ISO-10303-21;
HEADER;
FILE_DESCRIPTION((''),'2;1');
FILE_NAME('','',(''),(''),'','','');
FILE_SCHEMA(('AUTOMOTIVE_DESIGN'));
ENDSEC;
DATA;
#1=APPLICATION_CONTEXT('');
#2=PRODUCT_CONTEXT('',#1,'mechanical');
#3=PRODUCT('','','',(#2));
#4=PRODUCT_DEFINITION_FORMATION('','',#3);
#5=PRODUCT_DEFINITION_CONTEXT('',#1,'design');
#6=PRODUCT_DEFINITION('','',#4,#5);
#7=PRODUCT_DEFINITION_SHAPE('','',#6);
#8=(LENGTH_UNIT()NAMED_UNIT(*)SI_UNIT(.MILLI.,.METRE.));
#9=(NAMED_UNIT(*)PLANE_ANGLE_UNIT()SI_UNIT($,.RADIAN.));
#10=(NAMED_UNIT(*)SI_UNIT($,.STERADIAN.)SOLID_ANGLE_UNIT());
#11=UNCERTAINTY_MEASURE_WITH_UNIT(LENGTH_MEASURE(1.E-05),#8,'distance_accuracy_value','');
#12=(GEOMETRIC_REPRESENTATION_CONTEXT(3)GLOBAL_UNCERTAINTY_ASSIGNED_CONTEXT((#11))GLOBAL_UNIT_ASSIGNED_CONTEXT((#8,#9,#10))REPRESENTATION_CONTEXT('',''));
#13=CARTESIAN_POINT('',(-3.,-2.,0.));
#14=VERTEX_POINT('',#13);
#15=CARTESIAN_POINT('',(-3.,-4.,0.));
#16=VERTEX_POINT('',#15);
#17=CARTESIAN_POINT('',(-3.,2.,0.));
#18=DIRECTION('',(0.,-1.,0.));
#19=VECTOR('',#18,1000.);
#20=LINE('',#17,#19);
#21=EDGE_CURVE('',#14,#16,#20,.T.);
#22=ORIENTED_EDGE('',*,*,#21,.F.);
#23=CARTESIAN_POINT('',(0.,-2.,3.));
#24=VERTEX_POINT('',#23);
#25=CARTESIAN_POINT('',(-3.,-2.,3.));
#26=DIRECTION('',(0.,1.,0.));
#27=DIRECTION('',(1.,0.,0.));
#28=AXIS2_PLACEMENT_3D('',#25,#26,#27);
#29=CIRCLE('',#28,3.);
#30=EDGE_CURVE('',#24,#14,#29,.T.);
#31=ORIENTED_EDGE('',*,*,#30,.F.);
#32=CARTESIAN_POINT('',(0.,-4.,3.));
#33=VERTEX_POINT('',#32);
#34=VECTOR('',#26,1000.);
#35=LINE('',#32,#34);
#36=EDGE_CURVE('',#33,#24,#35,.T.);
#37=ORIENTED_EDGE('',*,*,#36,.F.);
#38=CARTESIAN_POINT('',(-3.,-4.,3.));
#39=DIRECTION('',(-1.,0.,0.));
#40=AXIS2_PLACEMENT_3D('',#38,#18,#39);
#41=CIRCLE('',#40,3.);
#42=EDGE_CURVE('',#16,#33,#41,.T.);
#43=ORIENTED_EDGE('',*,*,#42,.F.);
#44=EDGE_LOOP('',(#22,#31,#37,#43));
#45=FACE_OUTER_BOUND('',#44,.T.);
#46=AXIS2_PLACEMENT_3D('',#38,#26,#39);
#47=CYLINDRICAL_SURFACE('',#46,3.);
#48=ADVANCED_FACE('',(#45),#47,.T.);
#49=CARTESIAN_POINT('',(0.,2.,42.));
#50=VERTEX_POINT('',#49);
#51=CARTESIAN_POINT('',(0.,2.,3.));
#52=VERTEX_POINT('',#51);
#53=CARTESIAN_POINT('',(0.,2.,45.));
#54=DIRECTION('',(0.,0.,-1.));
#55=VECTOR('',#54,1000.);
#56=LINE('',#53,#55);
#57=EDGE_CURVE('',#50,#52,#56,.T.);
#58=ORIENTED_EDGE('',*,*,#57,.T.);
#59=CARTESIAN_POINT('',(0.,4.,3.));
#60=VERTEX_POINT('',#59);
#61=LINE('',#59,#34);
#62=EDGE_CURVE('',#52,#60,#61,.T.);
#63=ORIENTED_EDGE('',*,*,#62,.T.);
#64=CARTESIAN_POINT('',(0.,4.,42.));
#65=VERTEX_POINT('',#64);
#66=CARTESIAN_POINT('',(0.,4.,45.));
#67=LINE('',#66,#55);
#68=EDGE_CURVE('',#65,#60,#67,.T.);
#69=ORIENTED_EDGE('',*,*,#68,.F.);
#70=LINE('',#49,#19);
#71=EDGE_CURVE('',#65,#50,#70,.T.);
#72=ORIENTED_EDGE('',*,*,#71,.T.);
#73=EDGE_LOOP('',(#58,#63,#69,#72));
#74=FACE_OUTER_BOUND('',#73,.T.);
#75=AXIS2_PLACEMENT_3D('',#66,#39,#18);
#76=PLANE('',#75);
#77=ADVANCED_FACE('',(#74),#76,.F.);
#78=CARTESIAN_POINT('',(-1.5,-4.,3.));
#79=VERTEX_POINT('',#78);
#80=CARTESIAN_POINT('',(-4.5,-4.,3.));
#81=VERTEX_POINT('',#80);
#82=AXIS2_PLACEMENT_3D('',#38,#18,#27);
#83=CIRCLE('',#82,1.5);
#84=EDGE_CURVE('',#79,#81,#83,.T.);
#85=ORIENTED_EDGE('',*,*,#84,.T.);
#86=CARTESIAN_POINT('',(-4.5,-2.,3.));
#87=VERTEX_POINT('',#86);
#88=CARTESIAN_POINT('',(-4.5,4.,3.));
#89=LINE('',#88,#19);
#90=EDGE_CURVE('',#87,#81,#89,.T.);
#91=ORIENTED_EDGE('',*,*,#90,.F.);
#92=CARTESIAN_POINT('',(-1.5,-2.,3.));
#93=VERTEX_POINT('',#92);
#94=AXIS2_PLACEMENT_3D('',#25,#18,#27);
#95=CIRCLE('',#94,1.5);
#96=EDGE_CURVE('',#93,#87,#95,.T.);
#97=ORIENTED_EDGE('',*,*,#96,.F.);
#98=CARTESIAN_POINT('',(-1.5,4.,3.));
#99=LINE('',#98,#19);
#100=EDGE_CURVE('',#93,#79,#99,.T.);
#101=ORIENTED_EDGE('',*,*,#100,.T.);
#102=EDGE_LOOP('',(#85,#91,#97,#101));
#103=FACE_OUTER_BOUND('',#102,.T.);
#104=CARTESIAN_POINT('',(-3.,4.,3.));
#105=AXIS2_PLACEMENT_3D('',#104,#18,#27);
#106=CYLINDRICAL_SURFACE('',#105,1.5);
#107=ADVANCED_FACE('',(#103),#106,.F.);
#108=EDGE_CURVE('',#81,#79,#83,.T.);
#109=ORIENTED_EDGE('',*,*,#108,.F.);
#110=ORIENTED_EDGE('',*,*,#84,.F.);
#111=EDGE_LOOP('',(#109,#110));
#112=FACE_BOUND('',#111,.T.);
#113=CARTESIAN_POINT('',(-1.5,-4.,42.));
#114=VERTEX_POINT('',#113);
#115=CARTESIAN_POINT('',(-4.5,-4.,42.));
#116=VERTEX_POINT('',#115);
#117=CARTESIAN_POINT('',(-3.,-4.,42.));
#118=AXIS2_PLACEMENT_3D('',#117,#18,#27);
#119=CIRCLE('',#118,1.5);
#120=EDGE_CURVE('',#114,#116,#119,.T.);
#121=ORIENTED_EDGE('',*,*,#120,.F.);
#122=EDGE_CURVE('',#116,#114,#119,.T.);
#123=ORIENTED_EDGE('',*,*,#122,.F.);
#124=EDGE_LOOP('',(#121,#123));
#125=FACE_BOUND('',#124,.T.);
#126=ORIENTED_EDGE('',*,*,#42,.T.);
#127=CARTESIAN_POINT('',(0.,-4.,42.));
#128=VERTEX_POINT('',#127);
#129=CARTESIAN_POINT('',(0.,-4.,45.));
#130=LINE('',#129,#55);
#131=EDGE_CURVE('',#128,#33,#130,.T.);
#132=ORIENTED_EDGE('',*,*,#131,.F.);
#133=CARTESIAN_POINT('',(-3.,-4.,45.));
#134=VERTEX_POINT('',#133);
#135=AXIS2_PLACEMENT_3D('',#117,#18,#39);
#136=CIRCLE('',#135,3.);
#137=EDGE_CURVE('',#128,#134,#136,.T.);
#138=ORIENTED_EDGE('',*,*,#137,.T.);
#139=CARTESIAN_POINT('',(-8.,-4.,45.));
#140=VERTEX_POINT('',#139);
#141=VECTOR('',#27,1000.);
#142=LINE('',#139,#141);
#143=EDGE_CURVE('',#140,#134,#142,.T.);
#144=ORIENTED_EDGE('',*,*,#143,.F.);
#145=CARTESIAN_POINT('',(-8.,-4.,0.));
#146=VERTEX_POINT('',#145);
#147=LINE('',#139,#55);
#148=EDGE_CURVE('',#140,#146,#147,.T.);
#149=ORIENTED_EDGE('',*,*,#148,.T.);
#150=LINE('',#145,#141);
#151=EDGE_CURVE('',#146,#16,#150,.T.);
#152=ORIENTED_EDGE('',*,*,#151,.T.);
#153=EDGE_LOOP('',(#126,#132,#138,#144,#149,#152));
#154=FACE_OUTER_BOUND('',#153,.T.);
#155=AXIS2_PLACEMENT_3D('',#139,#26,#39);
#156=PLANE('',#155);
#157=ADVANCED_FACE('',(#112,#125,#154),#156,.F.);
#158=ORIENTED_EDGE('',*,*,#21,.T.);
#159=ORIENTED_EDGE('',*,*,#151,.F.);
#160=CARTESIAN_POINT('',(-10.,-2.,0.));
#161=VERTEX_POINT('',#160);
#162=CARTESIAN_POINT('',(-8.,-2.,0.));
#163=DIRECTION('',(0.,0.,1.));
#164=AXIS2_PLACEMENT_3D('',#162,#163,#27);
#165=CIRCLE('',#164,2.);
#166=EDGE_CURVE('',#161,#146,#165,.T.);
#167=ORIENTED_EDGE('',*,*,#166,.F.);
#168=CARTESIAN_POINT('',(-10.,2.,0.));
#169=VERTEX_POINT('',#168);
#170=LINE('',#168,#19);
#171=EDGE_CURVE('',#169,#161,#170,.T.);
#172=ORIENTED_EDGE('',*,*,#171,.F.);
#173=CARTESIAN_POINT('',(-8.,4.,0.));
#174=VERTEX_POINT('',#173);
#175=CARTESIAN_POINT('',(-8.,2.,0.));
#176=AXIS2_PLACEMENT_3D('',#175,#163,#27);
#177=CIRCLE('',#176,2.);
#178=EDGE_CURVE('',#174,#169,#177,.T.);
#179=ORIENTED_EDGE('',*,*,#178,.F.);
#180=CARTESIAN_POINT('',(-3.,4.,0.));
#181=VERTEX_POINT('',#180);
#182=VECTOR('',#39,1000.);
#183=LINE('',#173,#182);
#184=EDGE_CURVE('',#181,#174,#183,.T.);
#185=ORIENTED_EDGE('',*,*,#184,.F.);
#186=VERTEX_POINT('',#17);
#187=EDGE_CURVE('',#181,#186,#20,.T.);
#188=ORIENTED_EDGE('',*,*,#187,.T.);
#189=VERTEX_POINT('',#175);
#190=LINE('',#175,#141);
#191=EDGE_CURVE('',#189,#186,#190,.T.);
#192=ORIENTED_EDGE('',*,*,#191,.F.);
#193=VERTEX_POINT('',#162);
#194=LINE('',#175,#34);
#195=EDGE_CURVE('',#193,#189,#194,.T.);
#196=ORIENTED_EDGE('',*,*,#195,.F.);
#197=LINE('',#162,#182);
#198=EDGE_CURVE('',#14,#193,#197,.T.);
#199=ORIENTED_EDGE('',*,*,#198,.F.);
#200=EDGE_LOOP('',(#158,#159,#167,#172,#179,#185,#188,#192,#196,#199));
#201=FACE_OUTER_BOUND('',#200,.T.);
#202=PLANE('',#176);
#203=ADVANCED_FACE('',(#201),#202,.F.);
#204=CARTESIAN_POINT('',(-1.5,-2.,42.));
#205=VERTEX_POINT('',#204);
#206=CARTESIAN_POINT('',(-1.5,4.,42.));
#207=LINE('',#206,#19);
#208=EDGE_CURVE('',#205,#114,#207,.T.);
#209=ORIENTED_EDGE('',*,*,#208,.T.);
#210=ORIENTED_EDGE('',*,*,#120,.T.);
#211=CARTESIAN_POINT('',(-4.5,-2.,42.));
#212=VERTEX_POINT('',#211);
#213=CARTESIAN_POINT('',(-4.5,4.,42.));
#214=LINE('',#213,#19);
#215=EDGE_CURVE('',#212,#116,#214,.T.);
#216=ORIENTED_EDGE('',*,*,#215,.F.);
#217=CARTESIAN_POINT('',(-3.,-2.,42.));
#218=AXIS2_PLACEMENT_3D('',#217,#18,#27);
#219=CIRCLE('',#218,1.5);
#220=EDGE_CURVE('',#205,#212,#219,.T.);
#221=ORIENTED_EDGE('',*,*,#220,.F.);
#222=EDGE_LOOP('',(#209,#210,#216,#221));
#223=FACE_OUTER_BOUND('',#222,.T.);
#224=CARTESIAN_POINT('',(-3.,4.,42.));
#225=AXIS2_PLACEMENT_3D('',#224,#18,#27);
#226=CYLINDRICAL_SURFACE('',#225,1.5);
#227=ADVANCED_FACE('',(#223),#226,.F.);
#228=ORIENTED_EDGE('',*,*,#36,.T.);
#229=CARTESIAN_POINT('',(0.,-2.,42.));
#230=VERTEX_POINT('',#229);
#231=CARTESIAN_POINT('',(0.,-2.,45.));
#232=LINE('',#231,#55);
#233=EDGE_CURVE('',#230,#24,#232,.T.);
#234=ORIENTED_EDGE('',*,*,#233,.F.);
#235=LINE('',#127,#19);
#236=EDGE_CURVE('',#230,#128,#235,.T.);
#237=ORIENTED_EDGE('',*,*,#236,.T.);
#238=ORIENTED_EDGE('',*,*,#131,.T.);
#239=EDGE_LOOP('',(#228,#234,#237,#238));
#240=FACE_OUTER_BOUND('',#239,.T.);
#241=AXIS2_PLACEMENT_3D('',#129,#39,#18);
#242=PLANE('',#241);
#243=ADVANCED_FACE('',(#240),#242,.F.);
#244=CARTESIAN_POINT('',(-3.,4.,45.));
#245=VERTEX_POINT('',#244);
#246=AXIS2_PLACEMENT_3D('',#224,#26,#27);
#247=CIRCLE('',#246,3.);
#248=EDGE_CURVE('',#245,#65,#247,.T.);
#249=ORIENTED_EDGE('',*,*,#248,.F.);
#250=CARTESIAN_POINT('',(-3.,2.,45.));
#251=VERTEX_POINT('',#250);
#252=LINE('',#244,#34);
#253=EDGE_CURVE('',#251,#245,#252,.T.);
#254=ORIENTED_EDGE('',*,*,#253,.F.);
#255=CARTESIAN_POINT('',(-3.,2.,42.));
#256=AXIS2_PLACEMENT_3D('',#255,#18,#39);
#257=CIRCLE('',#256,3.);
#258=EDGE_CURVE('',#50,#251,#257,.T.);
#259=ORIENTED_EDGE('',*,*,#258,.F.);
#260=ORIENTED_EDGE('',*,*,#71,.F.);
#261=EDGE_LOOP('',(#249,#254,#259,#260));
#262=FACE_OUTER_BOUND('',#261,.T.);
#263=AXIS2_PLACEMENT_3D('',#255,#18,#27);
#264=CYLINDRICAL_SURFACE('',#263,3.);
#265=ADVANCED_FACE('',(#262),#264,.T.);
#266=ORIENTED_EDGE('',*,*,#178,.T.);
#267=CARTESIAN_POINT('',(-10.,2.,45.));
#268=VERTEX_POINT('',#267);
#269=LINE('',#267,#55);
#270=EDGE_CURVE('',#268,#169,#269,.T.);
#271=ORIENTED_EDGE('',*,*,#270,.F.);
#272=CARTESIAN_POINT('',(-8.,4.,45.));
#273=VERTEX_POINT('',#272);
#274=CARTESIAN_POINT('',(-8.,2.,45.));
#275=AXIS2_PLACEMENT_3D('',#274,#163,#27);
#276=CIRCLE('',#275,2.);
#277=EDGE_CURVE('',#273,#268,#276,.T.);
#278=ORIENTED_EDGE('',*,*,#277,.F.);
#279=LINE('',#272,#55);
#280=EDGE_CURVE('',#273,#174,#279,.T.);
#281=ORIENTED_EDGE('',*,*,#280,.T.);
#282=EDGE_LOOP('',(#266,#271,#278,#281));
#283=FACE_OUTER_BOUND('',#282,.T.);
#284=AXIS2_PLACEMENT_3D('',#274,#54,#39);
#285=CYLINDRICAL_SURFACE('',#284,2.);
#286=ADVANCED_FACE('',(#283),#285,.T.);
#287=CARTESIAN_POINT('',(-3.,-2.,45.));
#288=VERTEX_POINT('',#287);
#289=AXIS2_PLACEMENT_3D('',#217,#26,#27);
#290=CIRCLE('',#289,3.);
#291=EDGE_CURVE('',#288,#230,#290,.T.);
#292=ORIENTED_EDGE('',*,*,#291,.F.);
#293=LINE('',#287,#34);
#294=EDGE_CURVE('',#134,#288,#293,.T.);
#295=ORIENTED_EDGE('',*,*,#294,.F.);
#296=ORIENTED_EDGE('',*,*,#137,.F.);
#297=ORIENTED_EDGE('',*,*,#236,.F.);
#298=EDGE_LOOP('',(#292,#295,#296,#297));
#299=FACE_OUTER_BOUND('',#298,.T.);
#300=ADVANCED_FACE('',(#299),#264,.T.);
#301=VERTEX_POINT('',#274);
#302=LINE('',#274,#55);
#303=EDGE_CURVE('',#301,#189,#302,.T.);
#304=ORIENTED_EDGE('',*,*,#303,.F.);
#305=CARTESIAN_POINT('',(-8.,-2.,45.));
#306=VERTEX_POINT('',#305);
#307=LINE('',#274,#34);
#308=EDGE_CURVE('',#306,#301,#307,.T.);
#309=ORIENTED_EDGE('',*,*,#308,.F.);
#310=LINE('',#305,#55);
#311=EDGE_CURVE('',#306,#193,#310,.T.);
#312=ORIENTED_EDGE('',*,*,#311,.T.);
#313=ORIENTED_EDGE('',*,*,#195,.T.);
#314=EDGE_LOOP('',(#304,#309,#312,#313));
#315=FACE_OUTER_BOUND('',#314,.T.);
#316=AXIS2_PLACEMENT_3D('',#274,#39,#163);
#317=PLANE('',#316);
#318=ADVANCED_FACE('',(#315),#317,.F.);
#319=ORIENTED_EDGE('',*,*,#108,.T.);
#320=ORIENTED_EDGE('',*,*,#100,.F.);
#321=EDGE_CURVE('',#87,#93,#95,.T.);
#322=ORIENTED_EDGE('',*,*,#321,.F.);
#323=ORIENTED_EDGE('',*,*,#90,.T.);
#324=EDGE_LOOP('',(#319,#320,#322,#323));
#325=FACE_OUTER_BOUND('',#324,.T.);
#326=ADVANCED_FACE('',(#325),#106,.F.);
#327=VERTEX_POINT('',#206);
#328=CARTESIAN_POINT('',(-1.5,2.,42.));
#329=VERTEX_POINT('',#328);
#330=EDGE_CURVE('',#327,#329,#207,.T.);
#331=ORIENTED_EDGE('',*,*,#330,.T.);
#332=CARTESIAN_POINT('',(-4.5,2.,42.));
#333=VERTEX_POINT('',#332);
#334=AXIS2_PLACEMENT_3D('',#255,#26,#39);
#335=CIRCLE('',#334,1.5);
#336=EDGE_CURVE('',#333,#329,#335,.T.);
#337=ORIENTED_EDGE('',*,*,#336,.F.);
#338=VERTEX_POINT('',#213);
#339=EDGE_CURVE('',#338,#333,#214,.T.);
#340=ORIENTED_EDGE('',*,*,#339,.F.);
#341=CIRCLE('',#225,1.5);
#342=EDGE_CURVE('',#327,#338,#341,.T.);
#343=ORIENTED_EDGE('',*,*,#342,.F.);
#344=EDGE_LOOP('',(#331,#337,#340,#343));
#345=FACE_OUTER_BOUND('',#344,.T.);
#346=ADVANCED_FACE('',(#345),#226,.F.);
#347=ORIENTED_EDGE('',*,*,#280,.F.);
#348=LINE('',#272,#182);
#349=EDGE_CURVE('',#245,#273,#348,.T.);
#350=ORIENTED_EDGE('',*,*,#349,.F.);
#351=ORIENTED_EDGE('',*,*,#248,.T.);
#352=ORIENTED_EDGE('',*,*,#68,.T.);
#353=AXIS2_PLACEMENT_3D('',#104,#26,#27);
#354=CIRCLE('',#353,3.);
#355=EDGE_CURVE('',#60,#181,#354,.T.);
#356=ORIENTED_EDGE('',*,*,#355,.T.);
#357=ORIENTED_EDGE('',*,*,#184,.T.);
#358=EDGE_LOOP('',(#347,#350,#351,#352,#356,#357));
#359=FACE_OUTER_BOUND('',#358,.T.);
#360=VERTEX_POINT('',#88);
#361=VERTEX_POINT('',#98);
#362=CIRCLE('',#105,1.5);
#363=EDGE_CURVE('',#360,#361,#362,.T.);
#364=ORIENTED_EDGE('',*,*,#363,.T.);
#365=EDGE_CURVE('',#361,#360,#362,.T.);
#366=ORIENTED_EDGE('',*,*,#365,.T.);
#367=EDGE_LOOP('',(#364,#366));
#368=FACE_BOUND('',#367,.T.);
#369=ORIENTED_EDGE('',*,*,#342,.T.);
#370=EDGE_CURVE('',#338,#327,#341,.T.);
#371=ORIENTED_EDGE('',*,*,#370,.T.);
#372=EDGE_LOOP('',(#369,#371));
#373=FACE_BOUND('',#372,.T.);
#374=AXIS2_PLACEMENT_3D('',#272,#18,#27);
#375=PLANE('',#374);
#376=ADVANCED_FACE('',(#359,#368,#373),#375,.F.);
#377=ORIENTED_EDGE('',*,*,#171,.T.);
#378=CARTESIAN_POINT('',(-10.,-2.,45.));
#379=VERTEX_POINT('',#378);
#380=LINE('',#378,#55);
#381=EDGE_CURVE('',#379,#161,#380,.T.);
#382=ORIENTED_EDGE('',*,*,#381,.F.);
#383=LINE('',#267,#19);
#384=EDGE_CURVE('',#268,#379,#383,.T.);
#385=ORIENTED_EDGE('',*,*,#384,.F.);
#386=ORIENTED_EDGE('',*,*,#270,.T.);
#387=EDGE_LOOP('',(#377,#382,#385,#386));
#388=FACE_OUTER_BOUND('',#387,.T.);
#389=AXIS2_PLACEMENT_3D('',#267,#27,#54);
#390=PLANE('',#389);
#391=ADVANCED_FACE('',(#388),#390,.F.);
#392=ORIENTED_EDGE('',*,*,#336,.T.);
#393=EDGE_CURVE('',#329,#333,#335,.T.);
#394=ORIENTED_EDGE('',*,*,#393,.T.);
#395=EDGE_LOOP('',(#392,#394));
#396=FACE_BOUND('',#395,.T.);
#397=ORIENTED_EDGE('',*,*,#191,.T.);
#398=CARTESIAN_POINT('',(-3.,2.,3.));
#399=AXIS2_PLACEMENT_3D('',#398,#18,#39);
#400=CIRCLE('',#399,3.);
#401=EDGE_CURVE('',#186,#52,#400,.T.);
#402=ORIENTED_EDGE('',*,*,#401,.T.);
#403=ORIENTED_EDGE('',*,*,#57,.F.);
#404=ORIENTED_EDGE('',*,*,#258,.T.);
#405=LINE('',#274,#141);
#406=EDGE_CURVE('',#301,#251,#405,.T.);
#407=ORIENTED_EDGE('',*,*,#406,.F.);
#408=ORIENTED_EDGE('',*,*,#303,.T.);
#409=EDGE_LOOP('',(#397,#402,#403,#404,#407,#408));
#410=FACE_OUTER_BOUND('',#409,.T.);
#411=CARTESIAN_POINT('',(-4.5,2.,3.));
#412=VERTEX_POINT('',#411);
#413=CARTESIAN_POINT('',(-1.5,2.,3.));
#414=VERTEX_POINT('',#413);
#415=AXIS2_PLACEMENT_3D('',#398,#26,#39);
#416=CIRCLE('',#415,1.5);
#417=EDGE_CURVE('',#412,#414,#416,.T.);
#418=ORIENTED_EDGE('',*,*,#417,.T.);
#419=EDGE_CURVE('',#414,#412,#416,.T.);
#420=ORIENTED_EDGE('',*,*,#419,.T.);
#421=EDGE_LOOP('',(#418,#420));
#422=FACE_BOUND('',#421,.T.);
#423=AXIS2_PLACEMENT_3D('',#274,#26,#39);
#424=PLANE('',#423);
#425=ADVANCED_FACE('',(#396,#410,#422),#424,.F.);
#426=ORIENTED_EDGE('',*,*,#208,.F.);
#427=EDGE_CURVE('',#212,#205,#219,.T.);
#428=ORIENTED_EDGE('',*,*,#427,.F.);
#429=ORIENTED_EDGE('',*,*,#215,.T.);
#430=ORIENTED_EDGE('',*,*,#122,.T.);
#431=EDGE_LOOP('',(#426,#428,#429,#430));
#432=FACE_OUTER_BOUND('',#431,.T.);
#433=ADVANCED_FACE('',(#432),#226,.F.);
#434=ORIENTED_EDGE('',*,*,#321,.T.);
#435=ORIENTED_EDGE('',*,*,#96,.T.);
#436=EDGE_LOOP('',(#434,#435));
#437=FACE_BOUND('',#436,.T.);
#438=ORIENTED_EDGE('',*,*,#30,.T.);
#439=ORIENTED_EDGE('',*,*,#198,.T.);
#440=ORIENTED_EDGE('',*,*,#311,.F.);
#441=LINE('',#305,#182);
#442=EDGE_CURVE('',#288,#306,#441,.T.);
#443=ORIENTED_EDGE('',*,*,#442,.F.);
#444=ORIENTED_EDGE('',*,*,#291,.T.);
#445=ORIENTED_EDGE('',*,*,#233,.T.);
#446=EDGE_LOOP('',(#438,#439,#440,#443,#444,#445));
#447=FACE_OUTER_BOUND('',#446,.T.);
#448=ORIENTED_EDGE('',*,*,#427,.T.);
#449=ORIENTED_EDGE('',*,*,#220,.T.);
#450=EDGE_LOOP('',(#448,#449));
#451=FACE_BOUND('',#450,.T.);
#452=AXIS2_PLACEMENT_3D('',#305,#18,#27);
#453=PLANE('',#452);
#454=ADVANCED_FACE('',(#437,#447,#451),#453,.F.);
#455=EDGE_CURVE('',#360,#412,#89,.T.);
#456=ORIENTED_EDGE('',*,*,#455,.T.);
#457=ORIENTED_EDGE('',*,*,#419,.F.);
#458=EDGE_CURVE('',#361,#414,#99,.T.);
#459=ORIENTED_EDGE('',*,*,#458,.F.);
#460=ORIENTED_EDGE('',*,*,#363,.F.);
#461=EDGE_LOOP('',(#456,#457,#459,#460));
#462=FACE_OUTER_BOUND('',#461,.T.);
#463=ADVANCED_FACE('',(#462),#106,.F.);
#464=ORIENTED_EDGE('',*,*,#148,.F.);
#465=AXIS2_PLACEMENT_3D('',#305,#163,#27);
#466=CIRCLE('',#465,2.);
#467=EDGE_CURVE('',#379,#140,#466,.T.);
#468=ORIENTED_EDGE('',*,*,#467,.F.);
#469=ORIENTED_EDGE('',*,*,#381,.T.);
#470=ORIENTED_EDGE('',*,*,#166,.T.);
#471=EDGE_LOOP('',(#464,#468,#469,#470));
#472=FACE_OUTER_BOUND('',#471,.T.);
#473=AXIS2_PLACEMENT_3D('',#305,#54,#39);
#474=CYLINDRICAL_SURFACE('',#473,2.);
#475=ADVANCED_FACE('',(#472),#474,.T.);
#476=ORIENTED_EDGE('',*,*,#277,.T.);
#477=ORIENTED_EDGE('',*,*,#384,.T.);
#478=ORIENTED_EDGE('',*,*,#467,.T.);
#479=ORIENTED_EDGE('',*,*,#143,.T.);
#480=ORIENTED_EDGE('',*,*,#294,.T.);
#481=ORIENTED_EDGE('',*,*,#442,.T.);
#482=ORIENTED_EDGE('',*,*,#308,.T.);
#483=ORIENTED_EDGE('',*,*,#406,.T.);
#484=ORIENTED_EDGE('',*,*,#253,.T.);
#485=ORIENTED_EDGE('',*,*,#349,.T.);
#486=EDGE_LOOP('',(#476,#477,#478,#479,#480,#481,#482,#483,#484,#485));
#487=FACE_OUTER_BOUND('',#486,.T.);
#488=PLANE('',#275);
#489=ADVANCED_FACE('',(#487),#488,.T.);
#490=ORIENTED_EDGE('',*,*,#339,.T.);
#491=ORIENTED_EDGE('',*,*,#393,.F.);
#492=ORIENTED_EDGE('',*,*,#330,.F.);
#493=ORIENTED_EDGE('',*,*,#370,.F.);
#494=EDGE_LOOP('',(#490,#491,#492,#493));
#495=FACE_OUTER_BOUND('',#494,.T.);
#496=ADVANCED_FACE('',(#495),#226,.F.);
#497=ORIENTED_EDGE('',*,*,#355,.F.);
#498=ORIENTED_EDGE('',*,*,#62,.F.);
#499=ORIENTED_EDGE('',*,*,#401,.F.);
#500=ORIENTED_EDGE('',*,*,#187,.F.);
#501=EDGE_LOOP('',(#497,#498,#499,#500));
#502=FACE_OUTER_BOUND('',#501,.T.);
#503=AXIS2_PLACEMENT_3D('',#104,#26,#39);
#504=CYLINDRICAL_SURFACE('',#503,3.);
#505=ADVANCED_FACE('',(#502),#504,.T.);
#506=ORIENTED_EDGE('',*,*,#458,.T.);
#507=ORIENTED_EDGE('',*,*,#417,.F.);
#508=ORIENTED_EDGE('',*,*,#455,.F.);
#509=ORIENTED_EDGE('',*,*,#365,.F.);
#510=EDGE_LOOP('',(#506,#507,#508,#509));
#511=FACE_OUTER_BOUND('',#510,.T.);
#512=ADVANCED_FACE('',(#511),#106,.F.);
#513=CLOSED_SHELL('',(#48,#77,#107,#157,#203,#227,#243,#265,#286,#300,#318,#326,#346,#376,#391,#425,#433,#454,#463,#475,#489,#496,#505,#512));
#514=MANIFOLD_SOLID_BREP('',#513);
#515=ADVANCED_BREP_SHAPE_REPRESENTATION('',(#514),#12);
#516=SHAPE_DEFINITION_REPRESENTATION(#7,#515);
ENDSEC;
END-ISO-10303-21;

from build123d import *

# Parameters (mm, degrees)
BOSS_EXTRUDE1_DEPTH = 45
SKETCH2_R           = 1.5
CUT_EXTRUDE1_DEPTH  = 47.786750261
FILLET1_R           = 3


with BuildPart() as part:
    # Sketch1 → Boss-Extrude1 (new body)
    with BuildSketch(Plane.XY):
        with BuildLine():
            Line((0, 4), (0, 2))
            Line((0, 2), (-8, 2))
            Line((-8, 2), (-8, -2))
            Line((-8, -2), (0, -2))
            Line((0, -2), (0, -4))
            Line((0, -4), (-8, -4))
            ThreePointArc((-8, -4), (-9.414213562, -3.414213562), (-10, -2))
            Line((-10, -2), (-10, 2))
            ThreePointArc((-10, 2), (-9.414213562, 3.414213562), (-8, 4))
            Line((-8, 4), (0, 4))
        make_face()
    extrude(amount=BOSS_EXTRUDE1_DEPTH)

    # Sketch2 → Cut-Extrude1 (cut, through all)
    with BuildSketch(Plane(origin=(0, -4, 0), x_dir=(-1, 0, 0), z_dir=(0, -1, 0))):
        with Locations(Location((3, -3, 0), (0, 0, 180))):
            Circle(SKETCH2_R)
        with Locations(Location((3, -42, 0), (0, 0, 180))):
            Circle(SKETCH2_R)
    extrude(amount=-CUT_EXTRUDE1_DEPTH, mode=Mode.SUBTRACT)

    # Fillet1
    fillet1_edges = [part.edges().sort_by_distance(p)[0] for p in [
        (0, 3, 0),
        (0, -3, 0),
        (0, 3, 45),
        (0, -3, 45),
    ]]
    fillet(fillet1_edges, radius=FILLET1_R)


solid = part.part
